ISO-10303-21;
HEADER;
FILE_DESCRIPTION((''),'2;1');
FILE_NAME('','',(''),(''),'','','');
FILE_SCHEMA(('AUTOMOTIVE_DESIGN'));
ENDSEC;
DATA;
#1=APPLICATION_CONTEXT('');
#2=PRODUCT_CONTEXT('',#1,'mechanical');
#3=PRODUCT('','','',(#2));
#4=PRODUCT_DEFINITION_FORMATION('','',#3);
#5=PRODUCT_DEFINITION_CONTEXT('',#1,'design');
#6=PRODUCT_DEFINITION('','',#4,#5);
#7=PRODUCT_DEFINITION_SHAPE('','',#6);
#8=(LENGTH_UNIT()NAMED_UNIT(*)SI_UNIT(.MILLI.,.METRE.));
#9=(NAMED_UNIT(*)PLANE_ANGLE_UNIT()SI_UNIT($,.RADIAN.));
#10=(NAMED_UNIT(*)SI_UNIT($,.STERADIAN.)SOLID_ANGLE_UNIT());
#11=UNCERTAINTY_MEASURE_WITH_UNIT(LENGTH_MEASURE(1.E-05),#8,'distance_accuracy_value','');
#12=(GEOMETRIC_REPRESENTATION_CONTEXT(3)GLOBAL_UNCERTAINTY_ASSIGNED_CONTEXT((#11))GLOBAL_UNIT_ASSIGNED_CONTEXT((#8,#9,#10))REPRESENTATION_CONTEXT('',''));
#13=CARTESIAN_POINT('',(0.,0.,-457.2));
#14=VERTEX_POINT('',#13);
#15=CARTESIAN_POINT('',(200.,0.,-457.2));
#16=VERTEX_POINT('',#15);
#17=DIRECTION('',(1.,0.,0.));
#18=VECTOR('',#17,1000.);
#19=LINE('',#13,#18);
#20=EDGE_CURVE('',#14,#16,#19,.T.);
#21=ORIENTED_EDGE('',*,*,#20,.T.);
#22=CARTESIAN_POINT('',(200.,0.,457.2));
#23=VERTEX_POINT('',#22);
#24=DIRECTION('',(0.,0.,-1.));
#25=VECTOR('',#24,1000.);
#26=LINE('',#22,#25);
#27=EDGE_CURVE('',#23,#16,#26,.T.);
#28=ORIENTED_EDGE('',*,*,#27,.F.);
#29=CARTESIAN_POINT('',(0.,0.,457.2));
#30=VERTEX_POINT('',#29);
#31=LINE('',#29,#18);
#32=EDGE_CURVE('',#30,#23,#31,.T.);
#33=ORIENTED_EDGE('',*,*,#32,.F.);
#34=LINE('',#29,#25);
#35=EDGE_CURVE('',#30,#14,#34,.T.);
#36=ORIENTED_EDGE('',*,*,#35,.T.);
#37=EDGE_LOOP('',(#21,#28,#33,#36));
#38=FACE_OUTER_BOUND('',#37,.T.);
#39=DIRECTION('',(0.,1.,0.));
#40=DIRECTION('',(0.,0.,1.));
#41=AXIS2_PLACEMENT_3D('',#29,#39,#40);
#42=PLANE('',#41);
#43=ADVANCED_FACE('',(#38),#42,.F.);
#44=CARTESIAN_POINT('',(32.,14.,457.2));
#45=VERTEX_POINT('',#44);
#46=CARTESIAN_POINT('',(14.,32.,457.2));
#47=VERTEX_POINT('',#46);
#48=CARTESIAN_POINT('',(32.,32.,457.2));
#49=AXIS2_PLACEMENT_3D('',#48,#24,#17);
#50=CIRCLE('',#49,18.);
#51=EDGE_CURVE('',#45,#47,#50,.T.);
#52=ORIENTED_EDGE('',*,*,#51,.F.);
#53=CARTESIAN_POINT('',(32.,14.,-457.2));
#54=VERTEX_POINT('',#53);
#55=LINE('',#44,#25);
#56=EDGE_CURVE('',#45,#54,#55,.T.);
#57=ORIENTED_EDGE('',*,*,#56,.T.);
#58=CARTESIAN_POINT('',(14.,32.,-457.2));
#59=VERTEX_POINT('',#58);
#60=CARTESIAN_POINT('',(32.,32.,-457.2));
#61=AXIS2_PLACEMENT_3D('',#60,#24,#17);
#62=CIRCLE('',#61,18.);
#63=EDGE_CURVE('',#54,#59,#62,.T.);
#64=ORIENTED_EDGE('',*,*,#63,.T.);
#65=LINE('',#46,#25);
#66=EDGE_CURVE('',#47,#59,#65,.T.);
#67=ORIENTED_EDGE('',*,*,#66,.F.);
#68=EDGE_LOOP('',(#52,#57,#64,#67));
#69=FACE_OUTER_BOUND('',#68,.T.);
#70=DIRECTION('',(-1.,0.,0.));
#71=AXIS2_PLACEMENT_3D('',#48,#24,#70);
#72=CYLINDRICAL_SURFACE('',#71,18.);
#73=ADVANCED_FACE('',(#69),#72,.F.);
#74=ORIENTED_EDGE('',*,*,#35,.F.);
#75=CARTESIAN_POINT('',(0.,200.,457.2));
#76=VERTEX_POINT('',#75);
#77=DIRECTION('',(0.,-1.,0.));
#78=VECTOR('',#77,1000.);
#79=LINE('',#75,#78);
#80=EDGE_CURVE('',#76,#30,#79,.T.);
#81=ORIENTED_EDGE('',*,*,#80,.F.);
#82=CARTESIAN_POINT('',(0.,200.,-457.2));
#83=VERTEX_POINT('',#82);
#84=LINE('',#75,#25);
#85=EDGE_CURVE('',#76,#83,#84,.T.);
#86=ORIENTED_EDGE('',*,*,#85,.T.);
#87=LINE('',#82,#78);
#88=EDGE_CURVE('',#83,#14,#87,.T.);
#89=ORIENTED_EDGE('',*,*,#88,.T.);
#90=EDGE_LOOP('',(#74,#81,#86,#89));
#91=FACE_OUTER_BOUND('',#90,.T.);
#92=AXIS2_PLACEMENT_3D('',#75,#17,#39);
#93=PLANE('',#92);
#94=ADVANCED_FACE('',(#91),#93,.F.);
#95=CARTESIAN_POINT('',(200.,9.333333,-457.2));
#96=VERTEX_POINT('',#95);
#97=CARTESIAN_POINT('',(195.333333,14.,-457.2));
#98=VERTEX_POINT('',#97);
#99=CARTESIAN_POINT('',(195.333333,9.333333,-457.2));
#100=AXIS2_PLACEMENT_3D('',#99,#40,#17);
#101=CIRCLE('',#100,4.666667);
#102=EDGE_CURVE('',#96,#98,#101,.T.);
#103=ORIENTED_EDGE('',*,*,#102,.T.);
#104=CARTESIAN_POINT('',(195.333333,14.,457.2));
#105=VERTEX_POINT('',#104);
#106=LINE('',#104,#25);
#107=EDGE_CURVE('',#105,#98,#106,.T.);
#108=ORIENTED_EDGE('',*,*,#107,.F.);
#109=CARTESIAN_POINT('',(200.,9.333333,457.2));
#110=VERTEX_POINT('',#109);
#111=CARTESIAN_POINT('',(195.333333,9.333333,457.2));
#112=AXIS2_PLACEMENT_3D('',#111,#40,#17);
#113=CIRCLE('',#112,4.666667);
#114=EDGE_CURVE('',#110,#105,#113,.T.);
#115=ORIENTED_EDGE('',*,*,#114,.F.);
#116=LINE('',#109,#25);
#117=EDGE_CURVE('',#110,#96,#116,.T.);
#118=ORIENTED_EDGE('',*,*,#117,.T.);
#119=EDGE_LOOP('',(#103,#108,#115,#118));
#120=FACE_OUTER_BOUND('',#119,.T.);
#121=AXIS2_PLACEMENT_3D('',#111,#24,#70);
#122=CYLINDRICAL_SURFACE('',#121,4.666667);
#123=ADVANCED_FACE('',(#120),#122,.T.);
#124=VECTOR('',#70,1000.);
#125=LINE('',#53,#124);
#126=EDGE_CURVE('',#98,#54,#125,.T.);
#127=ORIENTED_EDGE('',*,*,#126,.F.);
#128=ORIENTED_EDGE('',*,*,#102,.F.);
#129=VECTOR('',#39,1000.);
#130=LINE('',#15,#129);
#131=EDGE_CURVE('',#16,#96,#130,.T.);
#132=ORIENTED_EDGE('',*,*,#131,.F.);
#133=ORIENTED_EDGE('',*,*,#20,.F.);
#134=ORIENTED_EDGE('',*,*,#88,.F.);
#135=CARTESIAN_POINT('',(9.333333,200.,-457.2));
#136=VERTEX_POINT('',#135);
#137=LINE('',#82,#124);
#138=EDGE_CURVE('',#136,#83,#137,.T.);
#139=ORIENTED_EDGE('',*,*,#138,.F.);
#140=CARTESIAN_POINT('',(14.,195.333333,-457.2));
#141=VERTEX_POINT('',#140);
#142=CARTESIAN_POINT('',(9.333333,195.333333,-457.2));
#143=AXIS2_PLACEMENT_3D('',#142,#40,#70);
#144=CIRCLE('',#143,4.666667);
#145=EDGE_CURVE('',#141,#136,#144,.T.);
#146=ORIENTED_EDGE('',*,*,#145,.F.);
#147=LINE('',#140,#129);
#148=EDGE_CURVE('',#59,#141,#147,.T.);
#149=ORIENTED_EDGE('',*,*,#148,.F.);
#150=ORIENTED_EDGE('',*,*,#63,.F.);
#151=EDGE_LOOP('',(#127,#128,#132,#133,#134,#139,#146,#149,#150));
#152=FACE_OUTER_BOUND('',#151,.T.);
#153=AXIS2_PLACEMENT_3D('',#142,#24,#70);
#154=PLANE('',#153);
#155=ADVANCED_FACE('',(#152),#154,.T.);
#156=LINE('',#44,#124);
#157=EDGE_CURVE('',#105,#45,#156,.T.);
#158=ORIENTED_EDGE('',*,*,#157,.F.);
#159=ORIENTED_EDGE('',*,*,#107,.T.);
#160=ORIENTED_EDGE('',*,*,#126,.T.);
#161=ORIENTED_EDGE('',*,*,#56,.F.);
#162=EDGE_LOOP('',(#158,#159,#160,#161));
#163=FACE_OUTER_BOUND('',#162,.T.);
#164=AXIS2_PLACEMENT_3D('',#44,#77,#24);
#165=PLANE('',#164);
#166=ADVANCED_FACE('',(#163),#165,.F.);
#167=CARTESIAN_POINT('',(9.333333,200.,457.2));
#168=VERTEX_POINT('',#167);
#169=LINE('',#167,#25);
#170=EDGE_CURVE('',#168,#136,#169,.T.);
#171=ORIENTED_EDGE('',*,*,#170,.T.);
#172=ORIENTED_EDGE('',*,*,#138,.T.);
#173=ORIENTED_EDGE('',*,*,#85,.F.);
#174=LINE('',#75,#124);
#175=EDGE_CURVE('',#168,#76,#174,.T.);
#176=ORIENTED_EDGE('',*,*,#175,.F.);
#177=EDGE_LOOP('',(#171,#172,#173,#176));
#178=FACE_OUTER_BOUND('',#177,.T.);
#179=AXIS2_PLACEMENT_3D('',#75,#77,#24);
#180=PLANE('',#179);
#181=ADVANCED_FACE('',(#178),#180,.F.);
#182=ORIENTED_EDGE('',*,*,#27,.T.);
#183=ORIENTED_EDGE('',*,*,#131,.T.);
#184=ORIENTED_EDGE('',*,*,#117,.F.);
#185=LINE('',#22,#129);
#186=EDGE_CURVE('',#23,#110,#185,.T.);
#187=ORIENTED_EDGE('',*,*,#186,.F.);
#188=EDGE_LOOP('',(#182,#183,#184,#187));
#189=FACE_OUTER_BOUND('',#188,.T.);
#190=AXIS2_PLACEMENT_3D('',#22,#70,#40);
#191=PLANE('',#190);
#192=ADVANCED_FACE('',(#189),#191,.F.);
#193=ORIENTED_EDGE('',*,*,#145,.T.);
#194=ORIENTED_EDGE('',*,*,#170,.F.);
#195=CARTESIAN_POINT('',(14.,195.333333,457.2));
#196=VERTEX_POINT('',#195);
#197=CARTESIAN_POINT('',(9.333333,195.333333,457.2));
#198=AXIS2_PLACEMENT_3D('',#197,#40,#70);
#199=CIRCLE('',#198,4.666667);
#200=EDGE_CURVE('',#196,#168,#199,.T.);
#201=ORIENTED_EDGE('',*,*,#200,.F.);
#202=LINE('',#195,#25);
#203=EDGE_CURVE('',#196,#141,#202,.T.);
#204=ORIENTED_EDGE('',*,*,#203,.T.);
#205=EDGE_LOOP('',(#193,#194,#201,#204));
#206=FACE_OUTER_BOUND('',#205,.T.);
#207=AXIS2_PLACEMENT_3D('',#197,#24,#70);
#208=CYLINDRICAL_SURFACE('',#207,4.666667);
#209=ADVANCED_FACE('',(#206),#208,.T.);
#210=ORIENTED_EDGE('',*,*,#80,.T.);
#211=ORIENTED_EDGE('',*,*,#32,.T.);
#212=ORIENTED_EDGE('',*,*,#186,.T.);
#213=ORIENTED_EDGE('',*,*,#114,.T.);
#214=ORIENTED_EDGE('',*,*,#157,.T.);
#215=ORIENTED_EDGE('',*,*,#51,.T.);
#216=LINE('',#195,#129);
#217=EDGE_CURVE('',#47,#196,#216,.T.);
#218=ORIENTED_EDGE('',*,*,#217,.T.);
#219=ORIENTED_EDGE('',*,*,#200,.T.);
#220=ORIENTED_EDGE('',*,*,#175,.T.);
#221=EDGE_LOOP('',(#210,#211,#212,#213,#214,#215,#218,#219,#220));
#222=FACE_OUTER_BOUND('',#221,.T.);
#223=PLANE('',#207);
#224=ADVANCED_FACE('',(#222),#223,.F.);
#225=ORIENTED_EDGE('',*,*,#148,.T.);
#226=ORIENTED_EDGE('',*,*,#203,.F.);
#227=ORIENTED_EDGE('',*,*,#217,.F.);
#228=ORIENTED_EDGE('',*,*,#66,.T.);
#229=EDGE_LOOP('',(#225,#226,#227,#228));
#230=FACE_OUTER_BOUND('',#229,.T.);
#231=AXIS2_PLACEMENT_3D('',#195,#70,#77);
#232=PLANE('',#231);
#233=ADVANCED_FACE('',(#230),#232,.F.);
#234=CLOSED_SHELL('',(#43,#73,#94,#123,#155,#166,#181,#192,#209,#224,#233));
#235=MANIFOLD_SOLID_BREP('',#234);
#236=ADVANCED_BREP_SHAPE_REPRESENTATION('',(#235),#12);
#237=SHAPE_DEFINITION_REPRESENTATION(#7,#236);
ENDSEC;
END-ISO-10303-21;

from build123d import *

# Parameters (mm, degrees)
BOSS_EXTRUDE1_DEPTH = 457.2


with BuildPart() as part:
    # Sketch1 → Boss-Extrude1 (new, symmetric)
    with BuildSketch(Plane.XY):
        with BuildLine():
            Line((0, 200), (0, 0))
            Line((0, 0), (200, 0))
            Line((200, 0), (200, 9.333333333))
            ThreePointArc((200, 9.333333333), (198.633164979, 12.633164979), (195.333333333, 14))
            Line((195.333333333, 14), (32, 14))
            ThreePointArc((32, 14), (19.272077939, 19.272077939), (14, 32))
            Line((14, 32), (14, 195.333333333))
            ThreePointArc((14, 195.333333333), (12.633164979, 198.633164979), (9.333333333, 200))
            Line((9.333333333, 200), (0, 200))
        make_face()
    extrude(amount=BOSS_EXTRUDE1_DEPTH, both=True)


solid = part.part
